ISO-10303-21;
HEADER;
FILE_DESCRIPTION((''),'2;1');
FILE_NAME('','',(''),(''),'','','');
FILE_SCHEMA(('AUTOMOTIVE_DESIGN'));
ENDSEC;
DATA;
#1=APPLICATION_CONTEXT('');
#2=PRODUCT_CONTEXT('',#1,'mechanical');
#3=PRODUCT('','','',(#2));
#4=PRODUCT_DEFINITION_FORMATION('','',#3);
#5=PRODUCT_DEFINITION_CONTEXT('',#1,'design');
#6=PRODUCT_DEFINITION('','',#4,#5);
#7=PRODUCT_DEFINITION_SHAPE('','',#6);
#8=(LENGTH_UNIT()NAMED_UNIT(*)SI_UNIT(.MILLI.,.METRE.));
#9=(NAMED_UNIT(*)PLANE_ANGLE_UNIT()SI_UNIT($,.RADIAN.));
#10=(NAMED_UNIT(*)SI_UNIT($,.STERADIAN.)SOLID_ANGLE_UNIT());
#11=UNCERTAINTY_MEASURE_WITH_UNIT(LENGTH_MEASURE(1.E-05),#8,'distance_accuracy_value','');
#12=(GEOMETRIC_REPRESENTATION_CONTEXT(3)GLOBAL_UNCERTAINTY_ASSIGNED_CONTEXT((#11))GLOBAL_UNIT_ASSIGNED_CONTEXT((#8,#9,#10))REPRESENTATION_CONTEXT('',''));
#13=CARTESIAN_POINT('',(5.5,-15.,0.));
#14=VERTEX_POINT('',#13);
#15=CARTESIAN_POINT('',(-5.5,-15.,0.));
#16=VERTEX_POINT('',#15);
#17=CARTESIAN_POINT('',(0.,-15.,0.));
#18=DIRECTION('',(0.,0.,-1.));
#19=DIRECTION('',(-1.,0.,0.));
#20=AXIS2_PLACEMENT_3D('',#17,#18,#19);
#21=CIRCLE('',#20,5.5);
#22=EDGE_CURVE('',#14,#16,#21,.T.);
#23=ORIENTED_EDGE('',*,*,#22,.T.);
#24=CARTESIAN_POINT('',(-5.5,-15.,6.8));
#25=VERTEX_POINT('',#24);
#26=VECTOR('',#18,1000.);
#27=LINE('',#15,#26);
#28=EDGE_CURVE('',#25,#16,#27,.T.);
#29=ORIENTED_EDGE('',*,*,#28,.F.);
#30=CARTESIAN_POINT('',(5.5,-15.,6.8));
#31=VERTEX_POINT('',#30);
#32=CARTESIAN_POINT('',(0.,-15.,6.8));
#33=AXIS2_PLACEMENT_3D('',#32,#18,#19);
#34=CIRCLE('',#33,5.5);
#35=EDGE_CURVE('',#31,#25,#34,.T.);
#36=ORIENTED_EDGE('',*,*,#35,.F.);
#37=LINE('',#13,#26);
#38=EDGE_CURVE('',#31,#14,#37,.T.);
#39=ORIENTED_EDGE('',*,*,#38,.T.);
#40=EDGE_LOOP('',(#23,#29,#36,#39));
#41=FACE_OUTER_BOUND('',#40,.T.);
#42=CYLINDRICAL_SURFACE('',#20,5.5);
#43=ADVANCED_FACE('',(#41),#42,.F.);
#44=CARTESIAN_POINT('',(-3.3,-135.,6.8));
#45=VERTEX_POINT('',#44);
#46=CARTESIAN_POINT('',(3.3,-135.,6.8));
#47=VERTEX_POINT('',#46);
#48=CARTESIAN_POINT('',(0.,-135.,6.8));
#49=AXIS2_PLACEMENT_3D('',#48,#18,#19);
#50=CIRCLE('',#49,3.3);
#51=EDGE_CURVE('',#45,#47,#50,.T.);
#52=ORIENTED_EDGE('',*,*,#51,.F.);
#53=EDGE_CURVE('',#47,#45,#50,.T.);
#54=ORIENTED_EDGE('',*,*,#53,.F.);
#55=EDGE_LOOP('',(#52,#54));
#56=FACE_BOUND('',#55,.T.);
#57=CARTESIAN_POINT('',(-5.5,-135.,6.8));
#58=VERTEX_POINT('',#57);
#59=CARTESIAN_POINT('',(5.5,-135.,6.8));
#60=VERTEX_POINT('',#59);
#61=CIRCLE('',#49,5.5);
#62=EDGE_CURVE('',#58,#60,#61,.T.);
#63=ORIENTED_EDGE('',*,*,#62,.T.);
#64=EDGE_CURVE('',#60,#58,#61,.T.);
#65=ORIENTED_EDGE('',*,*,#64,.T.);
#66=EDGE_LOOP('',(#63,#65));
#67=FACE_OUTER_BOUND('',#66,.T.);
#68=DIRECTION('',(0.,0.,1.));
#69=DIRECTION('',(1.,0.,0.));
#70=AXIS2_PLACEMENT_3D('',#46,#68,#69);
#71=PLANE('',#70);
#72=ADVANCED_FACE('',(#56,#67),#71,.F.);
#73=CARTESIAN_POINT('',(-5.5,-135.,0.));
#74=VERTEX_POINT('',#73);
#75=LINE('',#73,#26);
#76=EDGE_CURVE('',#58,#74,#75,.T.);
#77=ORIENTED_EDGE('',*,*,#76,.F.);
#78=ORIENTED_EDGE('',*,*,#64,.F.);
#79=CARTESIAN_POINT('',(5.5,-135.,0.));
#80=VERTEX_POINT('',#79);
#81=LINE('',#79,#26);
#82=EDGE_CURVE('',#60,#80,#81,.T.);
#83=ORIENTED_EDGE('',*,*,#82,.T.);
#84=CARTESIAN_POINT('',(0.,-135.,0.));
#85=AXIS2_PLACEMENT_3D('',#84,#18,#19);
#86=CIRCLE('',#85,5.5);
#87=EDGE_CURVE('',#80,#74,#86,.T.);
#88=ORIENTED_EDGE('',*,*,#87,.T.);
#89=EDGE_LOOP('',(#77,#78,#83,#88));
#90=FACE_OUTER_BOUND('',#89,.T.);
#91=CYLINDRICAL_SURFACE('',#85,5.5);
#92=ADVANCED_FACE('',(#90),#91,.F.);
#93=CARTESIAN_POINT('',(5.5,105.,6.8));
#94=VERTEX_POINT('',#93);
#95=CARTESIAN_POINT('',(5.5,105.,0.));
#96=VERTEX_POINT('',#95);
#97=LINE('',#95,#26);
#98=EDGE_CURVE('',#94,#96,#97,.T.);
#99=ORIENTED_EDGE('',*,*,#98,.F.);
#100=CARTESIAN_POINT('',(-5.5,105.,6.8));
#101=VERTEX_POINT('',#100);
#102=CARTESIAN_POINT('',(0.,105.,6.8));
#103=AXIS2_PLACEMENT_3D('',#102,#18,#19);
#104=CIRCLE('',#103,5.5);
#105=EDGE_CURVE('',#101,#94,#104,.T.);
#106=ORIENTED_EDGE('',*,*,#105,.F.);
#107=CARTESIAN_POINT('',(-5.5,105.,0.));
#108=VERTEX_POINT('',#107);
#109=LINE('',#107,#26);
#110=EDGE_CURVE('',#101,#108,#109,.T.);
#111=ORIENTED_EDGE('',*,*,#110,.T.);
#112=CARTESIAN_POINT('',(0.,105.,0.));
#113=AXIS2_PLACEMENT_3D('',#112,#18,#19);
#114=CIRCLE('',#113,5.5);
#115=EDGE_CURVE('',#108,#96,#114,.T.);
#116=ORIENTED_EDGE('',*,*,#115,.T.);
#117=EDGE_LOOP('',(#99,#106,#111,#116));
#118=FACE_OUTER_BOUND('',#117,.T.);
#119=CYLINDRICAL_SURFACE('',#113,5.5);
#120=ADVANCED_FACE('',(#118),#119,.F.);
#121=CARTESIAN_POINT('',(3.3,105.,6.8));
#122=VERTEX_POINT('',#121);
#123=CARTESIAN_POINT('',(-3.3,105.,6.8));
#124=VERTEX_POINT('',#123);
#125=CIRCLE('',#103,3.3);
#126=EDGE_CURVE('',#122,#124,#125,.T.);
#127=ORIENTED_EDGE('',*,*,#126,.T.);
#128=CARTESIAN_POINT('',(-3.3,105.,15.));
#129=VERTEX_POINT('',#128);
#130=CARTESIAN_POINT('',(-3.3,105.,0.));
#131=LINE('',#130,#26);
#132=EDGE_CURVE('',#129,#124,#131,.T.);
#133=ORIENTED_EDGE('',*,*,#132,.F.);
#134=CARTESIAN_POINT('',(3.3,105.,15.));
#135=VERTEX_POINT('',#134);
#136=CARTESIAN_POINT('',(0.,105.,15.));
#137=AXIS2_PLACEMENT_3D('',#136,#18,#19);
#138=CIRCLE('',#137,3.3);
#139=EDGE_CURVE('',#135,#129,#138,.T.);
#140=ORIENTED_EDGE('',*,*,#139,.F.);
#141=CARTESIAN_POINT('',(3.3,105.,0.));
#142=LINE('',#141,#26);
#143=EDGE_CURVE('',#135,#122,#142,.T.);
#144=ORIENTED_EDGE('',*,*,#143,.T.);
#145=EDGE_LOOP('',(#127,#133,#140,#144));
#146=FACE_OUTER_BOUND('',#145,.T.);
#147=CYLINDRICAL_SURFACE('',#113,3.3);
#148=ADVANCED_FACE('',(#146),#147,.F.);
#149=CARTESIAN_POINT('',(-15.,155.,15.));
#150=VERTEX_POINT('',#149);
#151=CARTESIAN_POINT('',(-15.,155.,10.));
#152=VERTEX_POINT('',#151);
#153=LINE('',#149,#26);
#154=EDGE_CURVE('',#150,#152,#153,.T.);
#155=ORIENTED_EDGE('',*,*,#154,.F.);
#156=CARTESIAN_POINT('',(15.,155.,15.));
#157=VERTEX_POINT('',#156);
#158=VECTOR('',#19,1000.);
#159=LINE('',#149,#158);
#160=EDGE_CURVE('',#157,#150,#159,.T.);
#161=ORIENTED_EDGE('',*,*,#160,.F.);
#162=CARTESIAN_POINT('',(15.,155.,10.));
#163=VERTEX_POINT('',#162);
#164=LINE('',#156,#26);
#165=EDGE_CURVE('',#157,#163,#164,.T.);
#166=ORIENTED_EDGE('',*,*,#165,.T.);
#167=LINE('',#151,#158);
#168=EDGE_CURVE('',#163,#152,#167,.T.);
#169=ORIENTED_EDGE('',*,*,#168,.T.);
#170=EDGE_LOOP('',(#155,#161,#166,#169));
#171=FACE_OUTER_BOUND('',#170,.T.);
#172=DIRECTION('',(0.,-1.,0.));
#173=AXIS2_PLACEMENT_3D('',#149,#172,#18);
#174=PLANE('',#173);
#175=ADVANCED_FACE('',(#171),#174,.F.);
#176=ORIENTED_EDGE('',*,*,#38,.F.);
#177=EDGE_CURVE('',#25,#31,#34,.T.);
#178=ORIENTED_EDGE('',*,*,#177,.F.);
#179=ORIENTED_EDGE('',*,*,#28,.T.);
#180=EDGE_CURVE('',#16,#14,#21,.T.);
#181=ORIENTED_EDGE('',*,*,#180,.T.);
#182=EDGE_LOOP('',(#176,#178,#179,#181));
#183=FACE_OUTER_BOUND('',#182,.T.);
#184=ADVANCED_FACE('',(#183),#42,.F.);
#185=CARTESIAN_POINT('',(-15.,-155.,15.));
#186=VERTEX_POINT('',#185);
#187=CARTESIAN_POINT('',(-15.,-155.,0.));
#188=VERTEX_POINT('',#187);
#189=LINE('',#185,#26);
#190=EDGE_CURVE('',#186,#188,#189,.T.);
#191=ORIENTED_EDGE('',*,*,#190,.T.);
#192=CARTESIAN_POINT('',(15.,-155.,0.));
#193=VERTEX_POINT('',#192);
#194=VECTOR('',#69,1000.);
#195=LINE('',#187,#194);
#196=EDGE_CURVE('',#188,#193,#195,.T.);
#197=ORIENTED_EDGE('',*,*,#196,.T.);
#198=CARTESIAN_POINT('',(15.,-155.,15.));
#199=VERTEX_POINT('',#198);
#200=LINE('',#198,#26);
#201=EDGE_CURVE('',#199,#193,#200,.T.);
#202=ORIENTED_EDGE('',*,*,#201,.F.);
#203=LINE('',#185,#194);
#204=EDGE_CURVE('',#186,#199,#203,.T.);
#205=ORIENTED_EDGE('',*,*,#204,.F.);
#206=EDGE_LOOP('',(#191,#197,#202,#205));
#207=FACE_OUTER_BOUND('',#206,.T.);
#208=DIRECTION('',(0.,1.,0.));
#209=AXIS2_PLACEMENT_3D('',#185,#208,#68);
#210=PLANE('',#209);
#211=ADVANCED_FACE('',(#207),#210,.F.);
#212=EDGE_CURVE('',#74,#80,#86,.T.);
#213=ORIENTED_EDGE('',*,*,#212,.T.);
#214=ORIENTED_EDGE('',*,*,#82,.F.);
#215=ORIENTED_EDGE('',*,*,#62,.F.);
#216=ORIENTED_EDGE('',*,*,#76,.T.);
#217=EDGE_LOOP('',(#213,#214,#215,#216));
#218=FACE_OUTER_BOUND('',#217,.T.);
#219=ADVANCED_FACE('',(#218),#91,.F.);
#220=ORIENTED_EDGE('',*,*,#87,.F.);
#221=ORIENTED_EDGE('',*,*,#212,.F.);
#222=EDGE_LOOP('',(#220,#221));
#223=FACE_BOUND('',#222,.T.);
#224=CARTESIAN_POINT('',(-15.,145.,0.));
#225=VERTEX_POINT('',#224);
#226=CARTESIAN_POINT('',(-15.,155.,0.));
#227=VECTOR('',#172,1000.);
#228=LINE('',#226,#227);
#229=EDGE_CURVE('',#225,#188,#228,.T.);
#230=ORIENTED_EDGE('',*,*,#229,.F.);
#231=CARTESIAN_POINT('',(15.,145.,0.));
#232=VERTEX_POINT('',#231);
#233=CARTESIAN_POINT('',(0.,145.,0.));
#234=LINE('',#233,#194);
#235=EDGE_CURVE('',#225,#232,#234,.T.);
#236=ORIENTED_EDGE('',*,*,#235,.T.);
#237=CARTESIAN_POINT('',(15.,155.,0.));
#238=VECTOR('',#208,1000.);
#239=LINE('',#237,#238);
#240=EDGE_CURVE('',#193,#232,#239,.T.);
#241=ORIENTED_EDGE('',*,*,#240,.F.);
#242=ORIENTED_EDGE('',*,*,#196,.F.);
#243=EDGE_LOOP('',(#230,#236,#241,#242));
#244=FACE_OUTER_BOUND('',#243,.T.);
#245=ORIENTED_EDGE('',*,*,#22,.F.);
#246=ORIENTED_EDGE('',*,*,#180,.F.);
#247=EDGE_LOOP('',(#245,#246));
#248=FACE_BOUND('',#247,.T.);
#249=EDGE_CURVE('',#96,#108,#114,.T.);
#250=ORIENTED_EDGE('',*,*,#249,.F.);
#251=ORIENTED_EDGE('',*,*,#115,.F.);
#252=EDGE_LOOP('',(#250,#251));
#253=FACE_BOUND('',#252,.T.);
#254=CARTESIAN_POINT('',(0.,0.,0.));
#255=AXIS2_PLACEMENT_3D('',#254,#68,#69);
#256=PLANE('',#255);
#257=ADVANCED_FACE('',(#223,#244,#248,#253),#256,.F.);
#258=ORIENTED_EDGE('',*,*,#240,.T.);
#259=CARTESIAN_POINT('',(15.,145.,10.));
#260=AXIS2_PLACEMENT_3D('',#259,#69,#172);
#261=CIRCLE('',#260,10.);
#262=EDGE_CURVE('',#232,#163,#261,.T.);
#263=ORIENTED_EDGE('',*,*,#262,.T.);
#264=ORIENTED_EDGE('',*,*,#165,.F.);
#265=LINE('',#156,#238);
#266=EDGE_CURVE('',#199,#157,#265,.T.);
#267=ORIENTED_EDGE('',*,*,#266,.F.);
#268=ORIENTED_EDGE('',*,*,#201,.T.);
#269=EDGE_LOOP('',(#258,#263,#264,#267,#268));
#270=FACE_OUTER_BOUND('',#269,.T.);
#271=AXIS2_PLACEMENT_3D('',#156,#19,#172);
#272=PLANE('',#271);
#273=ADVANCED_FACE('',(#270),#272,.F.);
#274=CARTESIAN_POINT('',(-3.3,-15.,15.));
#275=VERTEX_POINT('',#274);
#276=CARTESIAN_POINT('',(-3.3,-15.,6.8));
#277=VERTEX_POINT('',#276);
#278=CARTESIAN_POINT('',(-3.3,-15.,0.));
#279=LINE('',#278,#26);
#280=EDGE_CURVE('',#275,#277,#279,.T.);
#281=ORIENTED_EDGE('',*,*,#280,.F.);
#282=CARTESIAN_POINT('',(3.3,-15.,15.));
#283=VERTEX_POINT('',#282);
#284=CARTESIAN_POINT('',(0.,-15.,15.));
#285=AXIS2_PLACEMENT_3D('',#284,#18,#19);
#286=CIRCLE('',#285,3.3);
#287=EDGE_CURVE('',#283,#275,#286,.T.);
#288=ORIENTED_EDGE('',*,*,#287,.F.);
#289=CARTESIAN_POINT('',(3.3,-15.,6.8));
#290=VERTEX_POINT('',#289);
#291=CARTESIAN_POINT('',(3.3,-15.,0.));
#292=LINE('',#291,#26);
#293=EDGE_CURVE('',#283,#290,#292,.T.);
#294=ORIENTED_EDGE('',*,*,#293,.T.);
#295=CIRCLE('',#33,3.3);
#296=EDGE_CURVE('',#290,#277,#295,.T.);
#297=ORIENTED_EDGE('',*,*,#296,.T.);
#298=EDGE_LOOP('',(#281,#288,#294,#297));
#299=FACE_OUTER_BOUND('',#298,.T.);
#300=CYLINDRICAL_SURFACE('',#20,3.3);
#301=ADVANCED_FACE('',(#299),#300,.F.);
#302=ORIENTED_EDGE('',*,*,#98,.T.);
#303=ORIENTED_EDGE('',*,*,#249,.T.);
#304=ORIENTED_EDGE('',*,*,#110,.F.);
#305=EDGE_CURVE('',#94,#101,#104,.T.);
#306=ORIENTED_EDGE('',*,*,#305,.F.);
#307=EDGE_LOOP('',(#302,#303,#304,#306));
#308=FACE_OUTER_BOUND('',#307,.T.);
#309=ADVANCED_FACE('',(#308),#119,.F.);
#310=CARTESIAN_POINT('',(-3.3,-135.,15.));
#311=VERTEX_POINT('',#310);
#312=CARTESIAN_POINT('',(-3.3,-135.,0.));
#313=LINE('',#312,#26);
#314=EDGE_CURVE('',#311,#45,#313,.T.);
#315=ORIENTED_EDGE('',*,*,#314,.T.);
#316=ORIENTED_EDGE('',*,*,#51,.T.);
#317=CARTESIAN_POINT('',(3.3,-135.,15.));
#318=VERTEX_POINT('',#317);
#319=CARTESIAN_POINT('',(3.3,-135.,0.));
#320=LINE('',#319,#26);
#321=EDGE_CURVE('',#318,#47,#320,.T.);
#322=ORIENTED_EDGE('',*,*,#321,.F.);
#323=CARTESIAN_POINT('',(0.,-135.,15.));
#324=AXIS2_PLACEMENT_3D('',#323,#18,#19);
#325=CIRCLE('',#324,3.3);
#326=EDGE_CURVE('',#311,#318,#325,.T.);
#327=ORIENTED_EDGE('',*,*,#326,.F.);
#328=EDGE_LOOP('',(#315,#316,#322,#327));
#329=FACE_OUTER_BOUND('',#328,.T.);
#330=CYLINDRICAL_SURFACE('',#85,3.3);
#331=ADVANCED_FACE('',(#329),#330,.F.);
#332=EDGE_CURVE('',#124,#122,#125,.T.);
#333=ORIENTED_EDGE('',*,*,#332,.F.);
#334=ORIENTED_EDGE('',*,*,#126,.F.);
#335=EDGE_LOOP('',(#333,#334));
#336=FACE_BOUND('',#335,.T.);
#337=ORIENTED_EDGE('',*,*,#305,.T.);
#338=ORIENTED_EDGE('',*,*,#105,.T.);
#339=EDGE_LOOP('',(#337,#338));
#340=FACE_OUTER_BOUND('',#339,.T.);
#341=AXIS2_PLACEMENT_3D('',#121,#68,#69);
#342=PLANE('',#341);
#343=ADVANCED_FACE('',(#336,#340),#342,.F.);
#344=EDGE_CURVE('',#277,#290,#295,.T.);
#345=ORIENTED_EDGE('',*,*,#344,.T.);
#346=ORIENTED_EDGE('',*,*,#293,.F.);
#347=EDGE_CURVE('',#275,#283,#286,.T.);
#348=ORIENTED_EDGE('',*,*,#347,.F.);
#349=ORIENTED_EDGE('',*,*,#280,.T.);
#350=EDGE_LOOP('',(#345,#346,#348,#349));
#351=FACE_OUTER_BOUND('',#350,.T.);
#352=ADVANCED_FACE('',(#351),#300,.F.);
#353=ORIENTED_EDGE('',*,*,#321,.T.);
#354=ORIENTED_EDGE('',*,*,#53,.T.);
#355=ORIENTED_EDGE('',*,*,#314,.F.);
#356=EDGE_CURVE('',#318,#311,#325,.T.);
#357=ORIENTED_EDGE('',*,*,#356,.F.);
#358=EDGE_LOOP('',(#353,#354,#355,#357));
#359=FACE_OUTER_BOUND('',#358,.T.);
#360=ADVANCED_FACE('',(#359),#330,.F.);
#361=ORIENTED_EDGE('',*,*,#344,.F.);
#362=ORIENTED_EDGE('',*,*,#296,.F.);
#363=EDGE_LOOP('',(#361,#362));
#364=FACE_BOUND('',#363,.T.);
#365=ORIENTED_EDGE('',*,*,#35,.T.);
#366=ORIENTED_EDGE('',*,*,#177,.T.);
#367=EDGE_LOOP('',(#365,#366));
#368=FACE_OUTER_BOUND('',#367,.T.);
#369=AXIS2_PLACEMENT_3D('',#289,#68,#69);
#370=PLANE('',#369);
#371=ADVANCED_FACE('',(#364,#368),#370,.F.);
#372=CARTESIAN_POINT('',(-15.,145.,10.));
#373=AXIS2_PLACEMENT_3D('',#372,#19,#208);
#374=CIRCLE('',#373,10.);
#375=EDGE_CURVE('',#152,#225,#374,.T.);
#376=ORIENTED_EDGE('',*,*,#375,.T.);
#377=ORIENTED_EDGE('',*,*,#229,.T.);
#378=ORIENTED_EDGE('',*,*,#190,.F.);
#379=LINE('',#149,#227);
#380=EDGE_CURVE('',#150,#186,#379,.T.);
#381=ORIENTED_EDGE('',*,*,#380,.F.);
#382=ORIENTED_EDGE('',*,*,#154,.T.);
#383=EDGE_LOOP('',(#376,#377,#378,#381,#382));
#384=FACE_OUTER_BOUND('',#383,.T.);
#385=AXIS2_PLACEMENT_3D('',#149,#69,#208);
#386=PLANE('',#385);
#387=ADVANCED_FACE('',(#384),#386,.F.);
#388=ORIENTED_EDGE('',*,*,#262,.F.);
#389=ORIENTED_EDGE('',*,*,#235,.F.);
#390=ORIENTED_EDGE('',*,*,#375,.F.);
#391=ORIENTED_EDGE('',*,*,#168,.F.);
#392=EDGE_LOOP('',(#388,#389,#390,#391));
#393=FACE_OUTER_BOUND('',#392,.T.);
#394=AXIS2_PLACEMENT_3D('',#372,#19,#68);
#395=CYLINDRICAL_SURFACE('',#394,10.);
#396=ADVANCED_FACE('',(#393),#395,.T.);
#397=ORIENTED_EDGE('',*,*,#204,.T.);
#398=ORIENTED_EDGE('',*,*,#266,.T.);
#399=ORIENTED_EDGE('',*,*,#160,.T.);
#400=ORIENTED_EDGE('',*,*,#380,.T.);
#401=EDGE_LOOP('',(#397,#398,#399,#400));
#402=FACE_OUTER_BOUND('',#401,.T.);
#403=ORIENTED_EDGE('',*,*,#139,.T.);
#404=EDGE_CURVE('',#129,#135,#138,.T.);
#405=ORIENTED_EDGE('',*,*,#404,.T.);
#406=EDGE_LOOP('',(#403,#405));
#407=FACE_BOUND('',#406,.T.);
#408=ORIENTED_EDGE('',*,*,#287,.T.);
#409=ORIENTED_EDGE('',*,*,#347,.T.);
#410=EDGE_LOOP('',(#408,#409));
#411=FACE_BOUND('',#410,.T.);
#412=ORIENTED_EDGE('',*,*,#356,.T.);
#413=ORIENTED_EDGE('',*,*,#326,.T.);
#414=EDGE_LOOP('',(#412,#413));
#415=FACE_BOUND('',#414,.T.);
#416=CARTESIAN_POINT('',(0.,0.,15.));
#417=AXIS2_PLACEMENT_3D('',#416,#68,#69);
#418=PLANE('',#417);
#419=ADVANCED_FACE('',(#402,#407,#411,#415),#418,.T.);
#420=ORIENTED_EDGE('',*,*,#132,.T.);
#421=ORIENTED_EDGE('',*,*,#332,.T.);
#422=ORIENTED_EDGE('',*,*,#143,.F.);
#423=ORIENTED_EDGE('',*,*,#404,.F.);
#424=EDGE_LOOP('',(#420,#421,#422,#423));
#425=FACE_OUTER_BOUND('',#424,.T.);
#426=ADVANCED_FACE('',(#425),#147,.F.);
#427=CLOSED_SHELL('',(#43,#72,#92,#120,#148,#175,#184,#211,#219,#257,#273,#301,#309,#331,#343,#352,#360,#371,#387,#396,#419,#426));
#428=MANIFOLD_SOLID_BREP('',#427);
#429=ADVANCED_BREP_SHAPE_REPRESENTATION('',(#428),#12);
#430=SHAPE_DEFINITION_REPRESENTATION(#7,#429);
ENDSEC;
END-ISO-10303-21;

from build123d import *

# Parameters (mm, degrees)
SKETCH_1_W                = 30
SKETCH_1_H                = 310
EXTRUDE_1_DEPTH           = 15
HOLE_WIZARD_1_D           = 6.6
HOLE_WIZARD_1_CBORE_D     = 11
HOLE_WIZARD_1_CBORE_DEPTH = 6.8
FILLET_1_R                = 10


with BuildPart() as part:
    # 草图1 → 凸台-拉伸1 (new body)
    with BuildSketch(Plane.XY):
        Rectangle(SKETCH_1_W, SKETCH_1_H)
    extrude(amount=EXTRUDE_1_DEPTH)

    # 打孔尺寸(%根据)内六角圆柱头螺钉的类型1 (through all)
    with Locations(Plane(origin=(0, 0, 0), x_dir=(-1, 0, 0), z_dir=(0, 0, -1))):
        with Locations((0, 105), (0, -15), (0, -135)):
            CounterBoreHole(HOLE_WIZARD_1_D / 2, HOLE_WIZARD_1_CBORE_D / 2, HOLE_WIZARD_1_CBORE_DEPTH)

    # 圆角1
    fillet_1_edges = [part.edges().sort_by_distance(p)[0] for p in [
        (0, 155, 0),
    ]]
    fillet(fillet_1_edges, radius=FILLET_1_R)


solid = part.part
